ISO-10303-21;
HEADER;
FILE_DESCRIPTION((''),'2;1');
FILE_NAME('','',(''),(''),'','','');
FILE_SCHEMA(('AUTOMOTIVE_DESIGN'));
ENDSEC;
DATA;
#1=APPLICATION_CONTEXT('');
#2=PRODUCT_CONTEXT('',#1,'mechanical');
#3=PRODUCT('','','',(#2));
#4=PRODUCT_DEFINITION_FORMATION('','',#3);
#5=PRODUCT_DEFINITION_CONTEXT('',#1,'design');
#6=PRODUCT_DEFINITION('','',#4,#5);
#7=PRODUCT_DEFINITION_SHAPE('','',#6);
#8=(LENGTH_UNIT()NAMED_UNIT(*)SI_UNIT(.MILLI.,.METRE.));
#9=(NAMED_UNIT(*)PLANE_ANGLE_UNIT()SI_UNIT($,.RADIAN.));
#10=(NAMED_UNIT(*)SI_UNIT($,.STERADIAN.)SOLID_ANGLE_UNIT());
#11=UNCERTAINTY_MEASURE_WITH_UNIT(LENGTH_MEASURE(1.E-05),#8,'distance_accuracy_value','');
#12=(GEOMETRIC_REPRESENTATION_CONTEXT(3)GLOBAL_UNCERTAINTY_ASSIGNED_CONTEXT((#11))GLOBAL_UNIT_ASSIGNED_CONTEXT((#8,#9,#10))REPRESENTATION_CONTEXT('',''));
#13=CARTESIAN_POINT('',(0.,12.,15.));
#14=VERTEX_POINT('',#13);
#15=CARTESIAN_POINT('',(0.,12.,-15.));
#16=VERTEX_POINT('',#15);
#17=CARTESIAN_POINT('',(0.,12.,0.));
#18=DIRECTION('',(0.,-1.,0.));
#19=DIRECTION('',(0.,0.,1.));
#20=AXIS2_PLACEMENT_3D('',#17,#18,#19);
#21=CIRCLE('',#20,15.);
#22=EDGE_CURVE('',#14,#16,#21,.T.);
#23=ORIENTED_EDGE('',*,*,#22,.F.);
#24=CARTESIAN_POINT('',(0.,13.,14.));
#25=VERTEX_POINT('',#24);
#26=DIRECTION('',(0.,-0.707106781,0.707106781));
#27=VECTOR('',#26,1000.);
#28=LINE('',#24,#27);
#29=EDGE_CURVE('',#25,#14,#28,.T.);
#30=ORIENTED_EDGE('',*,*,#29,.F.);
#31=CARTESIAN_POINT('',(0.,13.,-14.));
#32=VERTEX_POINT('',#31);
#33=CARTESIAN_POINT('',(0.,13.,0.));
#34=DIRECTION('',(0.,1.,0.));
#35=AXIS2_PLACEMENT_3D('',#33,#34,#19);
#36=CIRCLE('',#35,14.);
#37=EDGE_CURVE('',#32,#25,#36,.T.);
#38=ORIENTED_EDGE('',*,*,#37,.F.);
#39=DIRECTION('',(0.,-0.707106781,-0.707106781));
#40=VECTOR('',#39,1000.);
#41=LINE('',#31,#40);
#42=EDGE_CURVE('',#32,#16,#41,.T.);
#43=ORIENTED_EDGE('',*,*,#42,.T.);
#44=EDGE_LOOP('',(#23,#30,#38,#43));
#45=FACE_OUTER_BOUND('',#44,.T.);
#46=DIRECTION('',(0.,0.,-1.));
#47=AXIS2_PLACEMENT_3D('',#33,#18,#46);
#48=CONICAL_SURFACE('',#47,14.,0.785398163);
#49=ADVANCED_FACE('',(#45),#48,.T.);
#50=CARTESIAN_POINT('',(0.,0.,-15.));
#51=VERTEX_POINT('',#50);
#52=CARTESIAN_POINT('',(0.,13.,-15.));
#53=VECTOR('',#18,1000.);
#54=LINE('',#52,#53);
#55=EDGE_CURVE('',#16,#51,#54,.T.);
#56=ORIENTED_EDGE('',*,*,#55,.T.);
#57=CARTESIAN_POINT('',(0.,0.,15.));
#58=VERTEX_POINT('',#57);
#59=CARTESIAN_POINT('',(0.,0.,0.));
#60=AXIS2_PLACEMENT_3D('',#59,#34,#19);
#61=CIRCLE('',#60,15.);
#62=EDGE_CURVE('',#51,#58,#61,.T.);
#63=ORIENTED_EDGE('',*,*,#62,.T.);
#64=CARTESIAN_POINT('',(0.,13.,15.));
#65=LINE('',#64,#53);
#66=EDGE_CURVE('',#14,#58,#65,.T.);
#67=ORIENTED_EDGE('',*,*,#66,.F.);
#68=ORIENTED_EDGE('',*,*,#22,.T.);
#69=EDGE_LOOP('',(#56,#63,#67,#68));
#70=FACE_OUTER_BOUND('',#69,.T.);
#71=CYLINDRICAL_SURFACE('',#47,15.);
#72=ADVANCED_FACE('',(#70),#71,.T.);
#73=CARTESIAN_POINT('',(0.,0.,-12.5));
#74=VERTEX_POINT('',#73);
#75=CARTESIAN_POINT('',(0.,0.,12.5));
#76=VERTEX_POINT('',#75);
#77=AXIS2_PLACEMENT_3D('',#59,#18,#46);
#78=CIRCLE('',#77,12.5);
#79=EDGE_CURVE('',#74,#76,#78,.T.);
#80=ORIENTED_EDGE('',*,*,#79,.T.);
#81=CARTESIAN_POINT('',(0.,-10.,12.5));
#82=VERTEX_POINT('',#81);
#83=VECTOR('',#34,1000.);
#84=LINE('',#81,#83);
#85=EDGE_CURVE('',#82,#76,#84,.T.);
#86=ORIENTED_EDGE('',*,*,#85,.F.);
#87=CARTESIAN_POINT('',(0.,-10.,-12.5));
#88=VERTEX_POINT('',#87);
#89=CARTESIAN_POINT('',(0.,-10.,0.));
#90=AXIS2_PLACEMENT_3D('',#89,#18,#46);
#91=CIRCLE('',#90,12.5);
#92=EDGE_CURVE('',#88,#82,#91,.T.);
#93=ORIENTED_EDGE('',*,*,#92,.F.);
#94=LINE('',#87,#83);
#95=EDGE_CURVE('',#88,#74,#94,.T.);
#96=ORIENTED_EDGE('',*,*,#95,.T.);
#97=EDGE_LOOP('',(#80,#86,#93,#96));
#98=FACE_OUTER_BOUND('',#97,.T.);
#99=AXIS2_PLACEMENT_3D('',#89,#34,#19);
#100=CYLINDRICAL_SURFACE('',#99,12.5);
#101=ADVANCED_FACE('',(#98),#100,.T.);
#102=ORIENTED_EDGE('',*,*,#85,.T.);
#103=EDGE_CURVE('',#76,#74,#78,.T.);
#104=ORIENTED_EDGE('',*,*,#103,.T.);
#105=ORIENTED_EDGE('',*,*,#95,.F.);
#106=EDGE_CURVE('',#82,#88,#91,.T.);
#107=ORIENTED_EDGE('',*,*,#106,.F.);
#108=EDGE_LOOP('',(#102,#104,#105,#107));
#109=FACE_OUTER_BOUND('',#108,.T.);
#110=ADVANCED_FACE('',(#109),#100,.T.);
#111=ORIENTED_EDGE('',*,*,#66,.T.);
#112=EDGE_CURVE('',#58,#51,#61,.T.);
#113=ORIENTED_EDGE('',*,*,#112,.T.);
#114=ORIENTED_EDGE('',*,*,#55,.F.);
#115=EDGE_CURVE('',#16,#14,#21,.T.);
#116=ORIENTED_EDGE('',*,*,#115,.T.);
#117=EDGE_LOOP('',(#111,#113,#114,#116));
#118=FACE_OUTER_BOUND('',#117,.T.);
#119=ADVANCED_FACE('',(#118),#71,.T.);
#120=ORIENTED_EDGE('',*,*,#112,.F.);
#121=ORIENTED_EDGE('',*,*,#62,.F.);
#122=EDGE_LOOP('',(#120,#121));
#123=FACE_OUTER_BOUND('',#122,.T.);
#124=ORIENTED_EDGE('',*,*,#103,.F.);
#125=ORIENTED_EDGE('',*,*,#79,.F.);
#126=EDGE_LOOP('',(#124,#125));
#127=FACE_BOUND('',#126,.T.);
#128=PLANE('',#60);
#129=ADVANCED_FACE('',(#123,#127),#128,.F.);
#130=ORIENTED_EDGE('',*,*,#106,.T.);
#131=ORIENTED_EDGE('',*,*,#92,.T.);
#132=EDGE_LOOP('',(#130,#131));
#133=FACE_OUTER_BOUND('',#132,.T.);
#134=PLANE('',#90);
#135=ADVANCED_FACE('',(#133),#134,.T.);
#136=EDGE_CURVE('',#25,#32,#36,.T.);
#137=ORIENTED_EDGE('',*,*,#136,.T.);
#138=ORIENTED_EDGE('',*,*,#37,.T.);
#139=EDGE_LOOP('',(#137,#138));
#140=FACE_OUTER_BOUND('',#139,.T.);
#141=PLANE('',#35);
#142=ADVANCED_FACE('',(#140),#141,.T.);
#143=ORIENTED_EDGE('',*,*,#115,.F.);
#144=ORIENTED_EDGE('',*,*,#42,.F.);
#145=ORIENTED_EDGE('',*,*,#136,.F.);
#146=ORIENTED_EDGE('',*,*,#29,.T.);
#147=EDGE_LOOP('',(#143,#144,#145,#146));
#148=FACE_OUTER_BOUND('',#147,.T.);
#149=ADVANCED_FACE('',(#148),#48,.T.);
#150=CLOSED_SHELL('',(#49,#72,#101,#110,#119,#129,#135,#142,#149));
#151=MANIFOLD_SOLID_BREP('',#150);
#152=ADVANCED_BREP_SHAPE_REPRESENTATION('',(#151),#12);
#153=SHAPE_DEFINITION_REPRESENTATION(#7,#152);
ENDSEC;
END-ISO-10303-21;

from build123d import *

# Parameters (mm, degrees)
SKETCH_1_R      = 15
EXTRUDE_1_DEPTH = 13
SKETCH_2_R      = 12.5
EXTRUDE_2_DEPTH = 10
CHAMFER_1_SIZE  = 1


with BuildPart() as part:
    # 草图1 → 凸台-拉伸1 (new body)
    with BuildSketch(Plane(origin=(0, 0, 0), x_dir=(1, 0, 0), z_dir=(0, 1, 0))):
        with Locations(Location((0, 0, 0), (0, 0, 90))):
            Circle(SKETCH_1_R)
    extrude(amount=EXTRUDE_1_DEPTH)

    # 草图2 → 凸台-拉伸2 (add)
    with BuildSketch(Plane.XZ):
        with Locations(Location((0, 0, 0), (0, 0, 270))):
            Circle(SKETCH_2_R)
    extrude(amount=EXTRUDE_2_DEPTH)

    # 倒角1
    chamfer_1_edges = [part.edges().sort_by_distance(p)[0] for p in [
        (0, 13, 15),
    ]]
    chamfer(chamfer_1_edges, length=CHAMFER_1_SIZE)


solid = part.part
